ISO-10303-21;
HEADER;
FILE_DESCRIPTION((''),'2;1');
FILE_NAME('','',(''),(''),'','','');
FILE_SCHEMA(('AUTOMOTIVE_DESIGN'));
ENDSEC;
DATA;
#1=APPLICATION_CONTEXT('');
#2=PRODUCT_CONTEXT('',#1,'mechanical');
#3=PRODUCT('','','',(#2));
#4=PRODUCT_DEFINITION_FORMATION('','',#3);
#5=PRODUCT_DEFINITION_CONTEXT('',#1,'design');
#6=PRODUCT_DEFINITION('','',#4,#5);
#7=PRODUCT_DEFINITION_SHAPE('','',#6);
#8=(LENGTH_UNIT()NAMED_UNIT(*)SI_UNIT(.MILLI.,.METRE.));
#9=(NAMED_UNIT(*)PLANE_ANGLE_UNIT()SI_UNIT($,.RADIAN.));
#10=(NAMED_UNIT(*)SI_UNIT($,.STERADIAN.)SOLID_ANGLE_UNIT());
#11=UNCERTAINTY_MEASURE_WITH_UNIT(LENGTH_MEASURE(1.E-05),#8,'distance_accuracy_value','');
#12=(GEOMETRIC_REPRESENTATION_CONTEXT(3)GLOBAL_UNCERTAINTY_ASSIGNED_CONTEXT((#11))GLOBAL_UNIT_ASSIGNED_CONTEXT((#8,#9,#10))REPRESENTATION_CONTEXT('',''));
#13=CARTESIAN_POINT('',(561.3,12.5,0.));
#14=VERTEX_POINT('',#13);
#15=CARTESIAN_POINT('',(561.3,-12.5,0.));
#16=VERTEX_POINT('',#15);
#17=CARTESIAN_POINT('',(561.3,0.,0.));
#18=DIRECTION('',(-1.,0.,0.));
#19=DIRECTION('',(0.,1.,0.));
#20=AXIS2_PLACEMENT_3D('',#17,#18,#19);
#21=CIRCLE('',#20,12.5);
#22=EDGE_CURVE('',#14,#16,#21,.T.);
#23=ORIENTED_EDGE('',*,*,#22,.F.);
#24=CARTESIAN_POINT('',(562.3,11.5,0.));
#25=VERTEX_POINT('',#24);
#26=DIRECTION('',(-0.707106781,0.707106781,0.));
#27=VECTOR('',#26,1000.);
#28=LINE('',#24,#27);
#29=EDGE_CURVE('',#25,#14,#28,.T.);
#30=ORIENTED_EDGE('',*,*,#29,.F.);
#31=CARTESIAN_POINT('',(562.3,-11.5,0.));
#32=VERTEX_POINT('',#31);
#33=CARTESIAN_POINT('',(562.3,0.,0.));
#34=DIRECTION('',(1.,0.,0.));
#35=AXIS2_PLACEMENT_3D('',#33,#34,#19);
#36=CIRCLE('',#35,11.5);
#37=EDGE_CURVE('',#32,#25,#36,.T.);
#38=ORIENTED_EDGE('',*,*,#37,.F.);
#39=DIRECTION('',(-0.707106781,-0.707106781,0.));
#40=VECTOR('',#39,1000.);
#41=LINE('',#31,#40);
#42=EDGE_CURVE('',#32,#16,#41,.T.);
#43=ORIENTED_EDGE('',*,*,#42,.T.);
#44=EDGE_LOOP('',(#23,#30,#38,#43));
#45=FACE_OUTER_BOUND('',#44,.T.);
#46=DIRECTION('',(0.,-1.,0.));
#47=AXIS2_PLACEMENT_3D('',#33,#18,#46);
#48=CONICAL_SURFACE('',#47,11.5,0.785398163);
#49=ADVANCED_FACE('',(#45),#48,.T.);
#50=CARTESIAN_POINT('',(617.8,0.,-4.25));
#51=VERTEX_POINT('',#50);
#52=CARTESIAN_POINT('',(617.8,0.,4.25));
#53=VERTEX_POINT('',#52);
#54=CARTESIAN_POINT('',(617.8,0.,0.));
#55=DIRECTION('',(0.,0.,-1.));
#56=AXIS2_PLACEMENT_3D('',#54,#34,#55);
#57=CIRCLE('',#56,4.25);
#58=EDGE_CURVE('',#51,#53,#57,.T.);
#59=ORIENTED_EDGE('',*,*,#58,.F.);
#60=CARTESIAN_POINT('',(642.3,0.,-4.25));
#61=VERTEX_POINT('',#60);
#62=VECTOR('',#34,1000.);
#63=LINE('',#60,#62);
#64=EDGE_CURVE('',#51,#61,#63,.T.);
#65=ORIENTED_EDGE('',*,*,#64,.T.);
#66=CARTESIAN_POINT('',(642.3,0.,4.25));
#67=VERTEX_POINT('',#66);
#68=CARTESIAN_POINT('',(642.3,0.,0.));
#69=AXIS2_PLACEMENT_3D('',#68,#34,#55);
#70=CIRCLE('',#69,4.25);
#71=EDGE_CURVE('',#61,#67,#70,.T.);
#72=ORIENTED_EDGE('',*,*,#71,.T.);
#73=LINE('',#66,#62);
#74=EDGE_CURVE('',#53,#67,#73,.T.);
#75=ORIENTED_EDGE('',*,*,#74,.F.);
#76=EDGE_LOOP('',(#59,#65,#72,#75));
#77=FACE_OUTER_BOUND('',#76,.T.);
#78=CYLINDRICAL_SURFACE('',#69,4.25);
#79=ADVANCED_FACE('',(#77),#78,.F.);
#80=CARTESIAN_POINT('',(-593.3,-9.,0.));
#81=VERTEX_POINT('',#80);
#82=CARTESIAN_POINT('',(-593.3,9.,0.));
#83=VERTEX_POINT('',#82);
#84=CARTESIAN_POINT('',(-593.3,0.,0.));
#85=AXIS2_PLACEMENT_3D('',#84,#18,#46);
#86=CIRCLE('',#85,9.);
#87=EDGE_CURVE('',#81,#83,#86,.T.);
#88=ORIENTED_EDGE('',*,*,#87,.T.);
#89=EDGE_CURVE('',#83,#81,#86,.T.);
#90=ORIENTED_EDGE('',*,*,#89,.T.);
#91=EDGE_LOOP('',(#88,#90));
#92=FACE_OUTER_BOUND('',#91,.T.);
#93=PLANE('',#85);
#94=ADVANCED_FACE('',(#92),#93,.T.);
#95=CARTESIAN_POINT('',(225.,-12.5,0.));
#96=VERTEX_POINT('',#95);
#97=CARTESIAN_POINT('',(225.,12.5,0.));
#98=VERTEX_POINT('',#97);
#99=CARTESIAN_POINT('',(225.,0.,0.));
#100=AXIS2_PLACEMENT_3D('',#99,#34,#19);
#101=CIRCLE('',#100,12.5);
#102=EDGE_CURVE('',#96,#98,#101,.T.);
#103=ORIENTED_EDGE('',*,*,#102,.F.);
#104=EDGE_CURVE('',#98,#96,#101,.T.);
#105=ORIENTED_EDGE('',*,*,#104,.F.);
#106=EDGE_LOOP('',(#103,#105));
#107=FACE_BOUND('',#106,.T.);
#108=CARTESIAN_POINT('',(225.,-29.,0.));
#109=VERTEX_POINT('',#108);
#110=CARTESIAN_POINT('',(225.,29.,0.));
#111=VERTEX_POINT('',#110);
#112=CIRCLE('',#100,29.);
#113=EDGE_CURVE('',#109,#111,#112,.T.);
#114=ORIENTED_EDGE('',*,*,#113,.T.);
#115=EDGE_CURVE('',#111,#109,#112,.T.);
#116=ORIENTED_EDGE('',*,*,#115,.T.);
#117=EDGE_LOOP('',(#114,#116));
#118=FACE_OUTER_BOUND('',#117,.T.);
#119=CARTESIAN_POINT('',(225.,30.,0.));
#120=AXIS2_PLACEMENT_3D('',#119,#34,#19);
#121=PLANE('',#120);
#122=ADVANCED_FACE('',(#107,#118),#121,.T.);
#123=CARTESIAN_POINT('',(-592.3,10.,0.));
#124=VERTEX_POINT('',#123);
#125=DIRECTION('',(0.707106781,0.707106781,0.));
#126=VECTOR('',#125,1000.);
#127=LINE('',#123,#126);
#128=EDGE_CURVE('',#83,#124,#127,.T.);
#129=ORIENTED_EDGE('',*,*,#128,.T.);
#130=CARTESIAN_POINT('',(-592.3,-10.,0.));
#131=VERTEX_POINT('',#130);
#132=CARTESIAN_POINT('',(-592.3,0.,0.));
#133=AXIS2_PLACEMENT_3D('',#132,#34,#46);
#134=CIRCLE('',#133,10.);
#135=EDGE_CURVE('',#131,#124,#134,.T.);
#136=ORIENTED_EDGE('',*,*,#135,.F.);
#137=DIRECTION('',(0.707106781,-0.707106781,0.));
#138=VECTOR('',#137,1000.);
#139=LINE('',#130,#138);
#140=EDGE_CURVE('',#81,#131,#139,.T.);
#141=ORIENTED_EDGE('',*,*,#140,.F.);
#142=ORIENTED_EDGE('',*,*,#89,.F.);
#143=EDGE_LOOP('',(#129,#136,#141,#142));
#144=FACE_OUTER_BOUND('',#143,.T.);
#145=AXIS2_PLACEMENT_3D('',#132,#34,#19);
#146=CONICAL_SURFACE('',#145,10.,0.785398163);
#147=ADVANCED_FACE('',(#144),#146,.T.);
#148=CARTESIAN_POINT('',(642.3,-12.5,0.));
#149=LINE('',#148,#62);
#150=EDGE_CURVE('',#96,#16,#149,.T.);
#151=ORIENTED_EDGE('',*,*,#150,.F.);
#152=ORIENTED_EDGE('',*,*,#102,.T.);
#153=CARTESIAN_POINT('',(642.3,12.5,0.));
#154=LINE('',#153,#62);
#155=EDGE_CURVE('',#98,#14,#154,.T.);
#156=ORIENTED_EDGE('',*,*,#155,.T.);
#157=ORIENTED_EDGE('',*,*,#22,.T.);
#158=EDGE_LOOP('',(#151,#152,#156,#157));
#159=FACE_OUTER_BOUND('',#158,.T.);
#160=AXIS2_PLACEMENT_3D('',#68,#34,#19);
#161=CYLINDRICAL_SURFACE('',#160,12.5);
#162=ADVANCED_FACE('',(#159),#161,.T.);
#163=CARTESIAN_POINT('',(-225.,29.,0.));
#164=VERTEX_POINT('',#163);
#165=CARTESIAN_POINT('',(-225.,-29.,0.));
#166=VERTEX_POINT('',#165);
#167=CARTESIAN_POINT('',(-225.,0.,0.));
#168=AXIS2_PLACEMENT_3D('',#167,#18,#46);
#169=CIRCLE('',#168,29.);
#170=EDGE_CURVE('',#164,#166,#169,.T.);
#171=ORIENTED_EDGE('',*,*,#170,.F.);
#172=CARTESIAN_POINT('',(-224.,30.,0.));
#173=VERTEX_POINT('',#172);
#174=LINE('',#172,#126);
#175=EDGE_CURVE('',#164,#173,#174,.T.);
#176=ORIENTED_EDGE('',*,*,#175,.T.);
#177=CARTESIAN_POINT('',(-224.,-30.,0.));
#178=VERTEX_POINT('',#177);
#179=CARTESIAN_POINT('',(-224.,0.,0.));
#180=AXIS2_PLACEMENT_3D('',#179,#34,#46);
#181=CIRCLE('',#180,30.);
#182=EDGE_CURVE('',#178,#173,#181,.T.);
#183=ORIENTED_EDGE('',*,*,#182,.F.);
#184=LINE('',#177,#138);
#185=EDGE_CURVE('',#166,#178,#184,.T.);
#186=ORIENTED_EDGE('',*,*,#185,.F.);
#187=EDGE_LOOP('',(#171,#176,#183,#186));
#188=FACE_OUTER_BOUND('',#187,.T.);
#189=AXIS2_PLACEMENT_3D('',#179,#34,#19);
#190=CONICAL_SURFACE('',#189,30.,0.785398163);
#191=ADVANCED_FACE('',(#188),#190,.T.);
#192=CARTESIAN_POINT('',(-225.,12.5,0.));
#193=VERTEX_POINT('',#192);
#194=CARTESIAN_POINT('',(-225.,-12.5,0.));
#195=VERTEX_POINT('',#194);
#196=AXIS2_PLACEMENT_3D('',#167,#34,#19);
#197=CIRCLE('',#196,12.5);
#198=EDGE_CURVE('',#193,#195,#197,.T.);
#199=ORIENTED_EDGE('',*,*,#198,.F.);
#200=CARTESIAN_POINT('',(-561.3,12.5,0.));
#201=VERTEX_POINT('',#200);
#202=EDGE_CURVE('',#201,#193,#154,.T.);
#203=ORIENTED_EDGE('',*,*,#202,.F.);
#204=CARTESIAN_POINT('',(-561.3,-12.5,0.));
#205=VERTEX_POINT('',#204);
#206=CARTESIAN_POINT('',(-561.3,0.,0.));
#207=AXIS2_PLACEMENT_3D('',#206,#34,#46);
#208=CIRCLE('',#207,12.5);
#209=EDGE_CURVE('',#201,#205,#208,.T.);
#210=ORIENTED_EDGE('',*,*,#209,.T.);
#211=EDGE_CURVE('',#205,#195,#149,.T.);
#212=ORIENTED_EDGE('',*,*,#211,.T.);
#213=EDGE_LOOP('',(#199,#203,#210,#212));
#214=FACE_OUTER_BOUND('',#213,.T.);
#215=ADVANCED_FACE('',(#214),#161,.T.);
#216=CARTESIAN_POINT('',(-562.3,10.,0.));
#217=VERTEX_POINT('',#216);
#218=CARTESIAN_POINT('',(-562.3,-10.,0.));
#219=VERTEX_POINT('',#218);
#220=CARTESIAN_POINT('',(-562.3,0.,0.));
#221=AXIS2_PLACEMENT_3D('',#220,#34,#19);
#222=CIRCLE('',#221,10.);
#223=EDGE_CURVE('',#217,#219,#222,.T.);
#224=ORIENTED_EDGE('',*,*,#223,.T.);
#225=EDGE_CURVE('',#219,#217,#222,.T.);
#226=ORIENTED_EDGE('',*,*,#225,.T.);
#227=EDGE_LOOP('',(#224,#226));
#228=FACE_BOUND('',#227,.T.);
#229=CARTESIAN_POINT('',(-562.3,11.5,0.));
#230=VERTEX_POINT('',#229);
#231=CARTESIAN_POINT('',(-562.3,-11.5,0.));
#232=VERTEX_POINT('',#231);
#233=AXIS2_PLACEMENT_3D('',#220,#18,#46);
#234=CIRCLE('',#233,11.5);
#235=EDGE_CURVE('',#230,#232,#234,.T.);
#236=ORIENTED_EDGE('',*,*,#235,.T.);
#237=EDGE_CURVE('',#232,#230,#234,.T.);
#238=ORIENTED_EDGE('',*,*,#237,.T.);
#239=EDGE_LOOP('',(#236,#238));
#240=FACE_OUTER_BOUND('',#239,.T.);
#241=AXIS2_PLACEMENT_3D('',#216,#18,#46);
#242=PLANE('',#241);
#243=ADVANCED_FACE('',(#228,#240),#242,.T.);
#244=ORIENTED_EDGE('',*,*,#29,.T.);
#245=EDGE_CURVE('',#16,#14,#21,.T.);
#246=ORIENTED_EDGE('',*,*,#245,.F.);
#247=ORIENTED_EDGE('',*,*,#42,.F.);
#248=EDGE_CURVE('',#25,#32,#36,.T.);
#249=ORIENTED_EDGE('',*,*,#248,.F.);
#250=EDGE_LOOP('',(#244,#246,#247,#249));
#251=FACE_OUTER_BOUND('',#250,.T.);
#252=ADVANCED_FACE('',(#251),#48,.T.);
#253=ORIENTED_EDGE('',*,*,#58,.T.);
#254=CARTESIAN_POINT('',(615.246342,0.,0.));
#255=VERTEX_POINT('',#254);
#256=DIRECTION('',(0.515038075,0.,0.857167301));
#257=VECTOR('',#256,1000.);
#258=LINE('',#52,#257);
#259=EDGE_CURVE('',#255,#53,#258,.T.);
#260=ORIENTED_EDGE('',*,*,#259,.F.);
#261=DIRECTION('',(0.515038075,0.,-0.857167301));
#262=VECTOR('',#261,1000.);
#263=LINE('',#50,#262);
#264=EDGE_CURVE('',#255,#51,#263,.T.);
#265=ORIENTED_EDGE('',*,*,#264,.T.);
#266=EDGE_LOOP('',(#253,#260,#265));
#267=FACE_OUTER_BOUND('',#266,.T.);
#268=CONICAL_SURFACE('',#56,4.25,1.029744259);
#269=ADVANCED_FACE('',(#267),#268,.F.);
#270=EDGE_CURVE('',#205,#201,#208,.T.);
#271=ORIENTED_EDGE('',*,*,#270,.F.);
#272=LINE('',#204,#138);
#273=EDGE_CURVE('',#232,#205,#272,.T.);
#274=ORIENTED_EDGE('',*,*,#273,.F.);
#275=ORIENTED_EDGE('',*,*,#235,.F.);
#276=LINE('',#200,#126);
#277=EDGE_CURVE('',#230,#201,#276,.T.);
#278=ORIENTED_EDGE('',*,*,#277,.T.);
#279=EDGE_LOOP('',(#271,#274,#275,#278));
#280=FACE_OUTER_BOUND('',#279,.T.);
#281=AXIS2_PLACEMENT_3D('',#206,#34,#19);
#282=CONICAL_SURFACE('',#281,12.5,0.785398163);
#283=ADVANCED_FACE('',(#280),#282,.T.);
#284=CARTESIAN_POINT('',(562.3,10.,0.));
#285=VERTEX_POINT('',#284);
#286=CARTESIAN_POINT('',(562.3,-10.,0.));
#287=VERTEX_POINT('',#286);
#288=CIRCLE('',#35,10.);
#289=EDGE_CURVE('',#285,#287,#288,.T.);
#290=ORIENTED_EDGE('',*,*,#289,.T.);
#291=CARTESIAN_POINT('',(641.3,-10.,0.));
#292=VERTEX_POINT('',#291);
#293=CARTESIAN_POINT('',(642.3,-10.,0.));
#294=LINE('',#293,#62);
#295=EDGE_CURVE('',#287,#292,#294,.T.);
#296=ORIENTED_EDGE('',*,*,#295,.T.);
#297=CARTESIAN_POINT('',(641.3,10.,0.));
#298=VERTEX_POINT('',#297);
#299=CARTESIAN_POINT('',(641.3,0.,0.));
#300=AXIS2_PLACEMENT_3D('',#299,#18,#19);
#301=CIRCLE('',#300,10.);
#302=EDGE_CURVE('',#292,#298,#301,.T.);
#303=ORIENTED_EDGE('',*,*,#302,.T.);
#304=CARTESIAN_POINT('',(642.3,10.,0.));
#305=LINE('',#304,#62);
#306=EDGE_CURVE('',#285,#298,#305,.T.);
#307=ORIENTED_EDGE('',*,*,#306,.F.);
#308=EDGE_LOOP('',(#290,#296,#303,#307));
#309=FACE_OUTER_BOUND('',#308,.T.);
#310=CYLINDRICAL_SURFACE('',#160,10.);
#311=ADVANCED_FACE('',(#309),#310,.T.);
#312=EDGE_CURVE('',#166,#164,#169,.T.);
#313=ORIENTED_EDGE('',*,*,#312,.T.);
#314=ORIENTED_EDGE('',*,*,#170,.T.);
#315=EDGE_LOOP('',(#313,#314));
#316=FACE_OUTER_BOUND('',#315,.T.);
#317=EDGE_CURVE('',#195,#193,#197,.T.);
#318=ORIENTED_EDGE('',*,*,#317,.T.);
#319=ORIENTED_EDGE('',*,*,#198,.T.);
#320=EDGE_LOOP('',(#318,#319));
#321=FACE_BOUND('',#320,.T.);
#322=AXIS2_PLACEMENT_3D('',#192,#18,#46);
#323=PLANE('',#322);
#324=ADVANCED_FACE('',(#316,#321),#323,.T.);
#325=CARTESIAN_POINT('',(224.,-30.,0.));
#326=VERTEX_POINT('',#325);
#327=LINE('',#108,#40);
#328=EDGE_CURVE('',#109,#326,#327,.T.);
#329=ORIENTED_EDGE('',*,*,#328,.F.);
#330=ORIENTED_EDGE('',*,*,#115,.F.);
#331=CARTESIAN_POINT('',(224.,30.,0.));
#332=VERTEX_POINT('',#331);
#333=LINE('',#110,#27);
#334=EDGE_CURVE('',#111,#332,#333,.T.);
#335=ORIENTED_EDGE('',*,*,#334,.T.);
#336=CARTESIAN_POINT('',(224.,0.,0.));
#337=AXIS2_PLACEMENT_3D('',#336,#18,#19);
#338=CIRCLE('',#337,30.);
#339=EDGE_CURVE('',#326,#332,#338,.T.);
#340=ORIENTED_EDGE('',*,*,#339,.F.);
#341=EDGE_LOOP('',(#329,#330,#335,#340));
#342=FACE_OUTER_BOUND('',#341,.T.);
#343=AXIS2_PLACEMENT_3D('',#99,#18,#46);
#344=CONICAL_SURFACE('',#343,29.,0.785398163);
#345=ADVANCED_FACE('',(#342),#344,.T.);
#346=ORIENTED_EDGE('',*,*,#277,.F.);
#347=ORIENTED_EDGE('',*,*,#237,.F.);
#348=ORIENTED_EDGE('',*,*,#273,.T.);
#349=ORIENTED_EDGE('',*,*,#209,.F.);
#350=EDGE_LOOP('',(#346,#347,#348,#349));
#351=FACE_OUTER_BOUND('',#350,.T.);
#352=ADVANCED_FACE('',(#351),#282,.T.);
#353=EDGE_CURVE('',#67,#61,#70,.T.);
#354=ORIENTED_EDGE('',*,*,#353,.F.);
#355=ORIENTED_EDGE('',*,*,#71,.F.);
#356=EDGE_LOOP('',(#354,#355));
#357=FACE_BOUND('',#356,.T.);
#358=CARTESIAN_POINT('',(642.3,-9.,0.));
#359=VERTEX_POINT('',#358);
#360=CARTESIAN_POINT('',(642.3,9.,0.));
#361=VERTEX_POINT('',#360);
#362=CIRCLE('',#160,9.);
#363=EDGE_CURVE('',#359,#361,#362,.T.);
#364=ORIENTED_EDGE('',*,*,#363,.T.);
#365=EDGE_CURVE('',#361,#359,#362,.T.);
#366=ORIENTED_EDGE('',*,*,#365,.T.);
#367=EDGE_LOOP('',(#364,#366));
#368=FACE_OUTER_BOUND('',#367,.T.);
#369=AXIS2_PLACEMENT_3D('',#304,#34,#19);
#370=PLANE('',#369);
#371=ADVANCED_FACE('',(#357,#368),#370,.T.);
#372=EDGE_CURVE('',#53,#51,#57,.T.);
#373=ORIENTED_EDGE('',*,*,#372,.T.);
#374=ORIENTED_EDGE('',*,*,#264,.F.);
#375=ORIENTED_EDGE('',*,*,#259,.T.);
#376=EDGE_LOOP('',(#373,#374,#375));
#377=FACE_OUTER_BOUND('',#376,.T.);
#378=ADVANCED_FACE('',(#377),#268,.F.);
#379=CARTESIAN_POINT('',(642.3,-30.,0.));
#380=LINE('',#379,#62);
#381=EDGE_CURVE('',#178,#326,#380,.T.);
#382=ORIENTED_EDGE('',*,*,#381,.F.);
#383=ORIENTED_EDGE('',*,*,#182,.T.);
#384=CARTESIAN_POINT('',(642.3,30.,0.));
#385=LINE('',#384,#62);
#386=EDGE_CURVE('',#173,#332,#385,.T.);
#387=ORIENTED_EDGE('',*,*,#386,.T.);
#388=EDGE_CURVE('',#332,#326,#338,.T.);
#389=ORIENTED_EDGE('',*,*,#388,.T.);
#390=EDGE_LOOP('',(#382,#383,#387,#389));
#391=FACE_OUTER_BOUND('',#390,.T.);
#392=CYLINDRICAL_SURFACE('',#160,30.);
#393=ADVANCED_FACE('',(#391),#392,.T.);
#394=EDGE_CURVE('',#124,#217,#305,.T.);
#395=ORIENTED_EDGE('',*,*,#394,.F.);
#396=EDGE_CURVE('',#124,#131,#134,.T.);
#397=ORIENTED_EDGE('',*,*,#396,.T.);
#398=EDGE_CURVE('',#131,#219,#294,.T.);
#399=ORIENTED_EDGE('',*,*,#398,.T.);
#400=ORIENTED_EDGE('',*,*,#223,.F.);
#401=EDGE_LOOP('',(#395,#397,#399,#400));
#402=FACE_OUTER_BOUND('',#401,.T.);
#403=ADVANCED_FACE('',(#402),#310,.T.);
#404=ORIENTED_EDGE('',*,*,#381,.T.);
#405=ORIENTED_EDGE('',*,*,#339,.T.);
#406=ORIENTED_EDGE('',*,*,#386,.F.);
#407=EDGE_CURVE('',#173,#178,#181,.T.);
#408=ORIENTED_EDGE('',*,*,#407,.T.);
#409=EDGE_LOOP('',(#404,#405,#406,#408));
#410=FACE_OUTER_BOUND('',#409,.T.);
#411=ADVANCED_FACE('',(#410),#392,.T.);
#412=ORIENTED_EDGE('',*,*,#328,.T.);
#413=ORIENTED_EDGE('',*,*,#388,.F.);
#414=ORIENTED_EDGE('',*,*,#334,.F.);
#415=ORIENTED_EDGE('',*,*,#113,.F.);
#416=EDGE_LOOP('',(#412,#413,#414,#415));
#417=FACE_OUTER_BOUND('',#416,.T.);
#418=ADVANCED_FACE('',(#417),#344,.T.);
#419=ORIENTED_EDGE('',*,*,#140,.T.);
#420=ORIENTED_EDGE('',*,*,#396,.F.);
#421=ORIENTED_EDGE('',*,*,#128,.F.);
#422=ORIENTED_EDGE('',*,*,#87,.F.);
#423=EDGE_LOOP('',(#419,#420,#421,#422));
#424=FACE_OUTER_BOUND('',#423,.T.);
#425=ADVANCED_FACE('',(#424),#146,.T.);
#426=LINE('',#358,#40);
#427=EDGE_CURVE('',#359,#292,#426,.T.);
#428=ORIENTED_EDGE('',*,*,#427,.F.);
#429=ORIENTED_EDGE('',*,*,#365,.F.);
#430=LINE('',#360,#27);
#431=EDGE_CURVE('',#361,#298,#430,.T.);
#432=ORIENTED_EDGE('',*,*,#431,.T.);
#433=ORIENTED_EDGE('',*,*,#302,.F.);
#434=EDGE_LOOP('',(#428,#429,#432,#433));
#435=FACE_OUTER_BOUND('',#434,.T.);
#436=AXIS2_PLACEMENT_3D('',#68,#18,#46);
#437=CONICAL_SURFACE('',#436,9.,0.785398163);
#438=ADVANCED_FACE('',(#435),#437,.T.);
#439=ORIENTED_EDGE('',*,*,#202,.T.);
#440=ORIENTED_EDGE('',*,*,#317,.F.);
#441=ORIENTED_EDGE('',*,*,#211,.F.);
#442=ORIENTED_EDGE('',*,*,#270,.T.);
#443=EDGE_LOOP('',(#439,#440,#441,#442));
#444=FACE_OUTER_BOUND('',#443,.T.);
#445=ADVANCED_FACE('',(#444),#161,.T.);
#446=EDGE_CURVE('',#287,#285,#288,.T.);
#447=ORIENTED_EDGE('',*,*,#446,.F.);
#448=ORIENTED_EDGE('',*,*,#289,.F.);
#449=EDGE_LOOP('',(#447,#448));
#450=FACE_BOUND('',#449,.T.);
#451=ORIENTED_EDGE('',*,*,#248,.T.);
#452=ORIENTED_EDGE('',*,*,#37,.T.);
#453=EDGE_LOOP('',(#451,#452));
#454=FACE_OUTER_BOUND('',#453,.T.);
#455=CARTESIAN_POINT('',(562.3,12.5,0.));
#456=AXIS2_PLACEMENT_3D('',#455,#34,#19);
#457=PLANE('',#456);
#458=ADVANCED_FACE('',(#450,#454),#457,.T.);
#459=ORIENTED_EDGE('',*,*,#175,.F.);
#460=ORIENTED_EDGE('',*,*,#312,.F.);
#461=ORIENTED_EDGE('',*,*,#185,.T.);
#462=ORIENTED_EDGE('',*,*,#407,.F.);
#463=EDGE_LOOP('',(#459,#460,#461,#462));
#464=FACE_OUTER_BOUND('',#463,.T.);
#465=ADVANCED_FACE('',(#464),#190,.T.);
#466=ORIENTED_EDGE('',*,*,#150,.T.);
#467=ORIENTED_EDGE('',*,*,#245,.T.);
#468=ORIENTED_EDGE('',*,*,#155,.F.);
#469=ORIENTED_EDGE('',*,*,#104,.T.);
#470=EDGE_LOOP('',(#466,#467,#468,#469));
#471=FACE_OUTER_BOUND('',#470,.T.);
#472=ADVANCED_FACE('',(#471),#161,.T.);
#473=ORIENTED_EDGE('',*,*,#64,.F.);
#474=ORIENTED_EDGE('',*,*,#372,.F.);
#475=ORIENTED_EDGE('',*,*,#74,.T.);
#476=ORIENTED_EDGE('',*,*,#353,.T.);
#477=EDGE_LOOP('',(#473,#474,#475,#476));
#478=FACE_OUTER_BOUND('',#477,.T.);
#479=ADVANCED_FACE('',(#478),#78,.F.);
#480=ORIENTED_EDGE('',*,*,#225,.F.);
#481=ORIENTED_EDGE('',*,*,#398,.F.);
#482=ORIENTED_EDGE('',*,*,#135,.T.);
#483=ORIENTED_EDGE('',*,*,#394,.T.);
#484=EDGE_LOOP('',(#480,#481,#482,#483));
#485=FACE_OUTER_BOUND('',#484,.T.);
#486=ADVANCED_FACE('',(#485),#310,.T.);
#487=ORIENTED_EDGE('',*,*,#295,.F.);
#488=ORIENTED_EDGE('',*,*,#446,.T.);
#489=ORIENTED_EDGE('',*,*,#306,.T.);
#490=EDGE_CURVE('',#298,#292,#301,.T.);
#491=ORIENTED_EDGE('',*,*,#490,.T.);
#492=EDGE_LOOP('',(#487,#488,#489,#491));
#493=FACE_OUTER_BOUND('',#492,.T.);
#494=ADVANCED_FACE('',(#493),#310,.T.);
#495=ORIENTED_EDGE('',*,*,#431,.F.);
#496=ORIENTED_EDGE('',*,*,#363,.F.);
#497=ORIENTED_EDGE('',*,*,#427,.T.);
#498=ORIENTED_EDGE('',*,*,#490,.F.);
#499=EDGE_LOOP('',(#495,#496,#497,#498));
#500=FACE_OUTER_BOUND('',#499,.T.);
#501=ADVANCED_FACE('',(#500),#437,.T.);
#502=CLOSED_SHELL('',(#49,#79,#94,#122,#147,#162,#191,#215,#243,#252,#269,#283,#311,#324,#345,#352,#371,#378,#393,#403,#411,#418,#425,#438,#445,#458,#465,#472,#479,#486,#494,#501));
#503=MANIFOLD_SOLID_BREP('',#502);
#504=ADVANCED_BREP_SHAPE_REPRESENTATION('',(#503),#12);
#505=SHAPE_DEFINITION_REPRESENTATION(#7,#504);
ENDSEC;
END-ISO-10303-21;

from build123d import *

# Parameters (mm, degrees)
CHAMFER_1_SIZE          = 1
HOLE_WIZARD_M10_1_D     = 8.5
HOLE_WIZARD_M10_1_DEPTH = 24.5
HOLE_WIZARD_M10_1_TIP   = 2.553657631


with BuildPart() as part:
    # 草图1 → 旋转1 (revolve)
    with BuildSketch(Plane.XY):
        Polygon((-593.3, 0), (-593.3, 10), (-562.3, 10), (-562.3, 12.5), (-225, 12.5), (-225, 30), (225, 30), (225, 12.5), (562.3, 12.5), (562.3, 10), (642.3, 10), (642.3, 0), align=None)
    revolve(axis=Axis((642.3, 0, 0), (-1, 0, 0)))

    # 倒角1
    chamfer_1_edges = [part.edges().sort_by_distance(p)[0] for p in [
        (225, -30, 0),
        (-225, -30, 0),
        (-562.3, -12.5, 0),
        (-593.3, -10, 0),
        (642.3, -10, 0),
        (562.3, -12.5, 0),
    ]]
    chamfer(chamfer_1_edges, length=CHAMFER_1_SIZE)

    # M10 螺纹孔1
    with Locations(Plane(origin=(642.3, 0, 0), x_dir=(0, 0, -1), z_dir=(1, 0, 0))):
        with Locations((0, 0)):
            Hole(HOLE_WIZARD_M10_1_D / 2, depth=HOLE_WIZARD_M10_1_DEPTH)
            with Locations((0, 0, -(HOLE_WIZARD_M10_1_DEPTH + HOLE_WIZARD_M10_1_TIP / 2))):  # 118° drill point
                Cone(0, HOLE_WIZARD_M10_1_D / 2, HOLE_WIZARD_M10_1_TIP, mode=Mode.SUBTRACT)


solid = part.part
